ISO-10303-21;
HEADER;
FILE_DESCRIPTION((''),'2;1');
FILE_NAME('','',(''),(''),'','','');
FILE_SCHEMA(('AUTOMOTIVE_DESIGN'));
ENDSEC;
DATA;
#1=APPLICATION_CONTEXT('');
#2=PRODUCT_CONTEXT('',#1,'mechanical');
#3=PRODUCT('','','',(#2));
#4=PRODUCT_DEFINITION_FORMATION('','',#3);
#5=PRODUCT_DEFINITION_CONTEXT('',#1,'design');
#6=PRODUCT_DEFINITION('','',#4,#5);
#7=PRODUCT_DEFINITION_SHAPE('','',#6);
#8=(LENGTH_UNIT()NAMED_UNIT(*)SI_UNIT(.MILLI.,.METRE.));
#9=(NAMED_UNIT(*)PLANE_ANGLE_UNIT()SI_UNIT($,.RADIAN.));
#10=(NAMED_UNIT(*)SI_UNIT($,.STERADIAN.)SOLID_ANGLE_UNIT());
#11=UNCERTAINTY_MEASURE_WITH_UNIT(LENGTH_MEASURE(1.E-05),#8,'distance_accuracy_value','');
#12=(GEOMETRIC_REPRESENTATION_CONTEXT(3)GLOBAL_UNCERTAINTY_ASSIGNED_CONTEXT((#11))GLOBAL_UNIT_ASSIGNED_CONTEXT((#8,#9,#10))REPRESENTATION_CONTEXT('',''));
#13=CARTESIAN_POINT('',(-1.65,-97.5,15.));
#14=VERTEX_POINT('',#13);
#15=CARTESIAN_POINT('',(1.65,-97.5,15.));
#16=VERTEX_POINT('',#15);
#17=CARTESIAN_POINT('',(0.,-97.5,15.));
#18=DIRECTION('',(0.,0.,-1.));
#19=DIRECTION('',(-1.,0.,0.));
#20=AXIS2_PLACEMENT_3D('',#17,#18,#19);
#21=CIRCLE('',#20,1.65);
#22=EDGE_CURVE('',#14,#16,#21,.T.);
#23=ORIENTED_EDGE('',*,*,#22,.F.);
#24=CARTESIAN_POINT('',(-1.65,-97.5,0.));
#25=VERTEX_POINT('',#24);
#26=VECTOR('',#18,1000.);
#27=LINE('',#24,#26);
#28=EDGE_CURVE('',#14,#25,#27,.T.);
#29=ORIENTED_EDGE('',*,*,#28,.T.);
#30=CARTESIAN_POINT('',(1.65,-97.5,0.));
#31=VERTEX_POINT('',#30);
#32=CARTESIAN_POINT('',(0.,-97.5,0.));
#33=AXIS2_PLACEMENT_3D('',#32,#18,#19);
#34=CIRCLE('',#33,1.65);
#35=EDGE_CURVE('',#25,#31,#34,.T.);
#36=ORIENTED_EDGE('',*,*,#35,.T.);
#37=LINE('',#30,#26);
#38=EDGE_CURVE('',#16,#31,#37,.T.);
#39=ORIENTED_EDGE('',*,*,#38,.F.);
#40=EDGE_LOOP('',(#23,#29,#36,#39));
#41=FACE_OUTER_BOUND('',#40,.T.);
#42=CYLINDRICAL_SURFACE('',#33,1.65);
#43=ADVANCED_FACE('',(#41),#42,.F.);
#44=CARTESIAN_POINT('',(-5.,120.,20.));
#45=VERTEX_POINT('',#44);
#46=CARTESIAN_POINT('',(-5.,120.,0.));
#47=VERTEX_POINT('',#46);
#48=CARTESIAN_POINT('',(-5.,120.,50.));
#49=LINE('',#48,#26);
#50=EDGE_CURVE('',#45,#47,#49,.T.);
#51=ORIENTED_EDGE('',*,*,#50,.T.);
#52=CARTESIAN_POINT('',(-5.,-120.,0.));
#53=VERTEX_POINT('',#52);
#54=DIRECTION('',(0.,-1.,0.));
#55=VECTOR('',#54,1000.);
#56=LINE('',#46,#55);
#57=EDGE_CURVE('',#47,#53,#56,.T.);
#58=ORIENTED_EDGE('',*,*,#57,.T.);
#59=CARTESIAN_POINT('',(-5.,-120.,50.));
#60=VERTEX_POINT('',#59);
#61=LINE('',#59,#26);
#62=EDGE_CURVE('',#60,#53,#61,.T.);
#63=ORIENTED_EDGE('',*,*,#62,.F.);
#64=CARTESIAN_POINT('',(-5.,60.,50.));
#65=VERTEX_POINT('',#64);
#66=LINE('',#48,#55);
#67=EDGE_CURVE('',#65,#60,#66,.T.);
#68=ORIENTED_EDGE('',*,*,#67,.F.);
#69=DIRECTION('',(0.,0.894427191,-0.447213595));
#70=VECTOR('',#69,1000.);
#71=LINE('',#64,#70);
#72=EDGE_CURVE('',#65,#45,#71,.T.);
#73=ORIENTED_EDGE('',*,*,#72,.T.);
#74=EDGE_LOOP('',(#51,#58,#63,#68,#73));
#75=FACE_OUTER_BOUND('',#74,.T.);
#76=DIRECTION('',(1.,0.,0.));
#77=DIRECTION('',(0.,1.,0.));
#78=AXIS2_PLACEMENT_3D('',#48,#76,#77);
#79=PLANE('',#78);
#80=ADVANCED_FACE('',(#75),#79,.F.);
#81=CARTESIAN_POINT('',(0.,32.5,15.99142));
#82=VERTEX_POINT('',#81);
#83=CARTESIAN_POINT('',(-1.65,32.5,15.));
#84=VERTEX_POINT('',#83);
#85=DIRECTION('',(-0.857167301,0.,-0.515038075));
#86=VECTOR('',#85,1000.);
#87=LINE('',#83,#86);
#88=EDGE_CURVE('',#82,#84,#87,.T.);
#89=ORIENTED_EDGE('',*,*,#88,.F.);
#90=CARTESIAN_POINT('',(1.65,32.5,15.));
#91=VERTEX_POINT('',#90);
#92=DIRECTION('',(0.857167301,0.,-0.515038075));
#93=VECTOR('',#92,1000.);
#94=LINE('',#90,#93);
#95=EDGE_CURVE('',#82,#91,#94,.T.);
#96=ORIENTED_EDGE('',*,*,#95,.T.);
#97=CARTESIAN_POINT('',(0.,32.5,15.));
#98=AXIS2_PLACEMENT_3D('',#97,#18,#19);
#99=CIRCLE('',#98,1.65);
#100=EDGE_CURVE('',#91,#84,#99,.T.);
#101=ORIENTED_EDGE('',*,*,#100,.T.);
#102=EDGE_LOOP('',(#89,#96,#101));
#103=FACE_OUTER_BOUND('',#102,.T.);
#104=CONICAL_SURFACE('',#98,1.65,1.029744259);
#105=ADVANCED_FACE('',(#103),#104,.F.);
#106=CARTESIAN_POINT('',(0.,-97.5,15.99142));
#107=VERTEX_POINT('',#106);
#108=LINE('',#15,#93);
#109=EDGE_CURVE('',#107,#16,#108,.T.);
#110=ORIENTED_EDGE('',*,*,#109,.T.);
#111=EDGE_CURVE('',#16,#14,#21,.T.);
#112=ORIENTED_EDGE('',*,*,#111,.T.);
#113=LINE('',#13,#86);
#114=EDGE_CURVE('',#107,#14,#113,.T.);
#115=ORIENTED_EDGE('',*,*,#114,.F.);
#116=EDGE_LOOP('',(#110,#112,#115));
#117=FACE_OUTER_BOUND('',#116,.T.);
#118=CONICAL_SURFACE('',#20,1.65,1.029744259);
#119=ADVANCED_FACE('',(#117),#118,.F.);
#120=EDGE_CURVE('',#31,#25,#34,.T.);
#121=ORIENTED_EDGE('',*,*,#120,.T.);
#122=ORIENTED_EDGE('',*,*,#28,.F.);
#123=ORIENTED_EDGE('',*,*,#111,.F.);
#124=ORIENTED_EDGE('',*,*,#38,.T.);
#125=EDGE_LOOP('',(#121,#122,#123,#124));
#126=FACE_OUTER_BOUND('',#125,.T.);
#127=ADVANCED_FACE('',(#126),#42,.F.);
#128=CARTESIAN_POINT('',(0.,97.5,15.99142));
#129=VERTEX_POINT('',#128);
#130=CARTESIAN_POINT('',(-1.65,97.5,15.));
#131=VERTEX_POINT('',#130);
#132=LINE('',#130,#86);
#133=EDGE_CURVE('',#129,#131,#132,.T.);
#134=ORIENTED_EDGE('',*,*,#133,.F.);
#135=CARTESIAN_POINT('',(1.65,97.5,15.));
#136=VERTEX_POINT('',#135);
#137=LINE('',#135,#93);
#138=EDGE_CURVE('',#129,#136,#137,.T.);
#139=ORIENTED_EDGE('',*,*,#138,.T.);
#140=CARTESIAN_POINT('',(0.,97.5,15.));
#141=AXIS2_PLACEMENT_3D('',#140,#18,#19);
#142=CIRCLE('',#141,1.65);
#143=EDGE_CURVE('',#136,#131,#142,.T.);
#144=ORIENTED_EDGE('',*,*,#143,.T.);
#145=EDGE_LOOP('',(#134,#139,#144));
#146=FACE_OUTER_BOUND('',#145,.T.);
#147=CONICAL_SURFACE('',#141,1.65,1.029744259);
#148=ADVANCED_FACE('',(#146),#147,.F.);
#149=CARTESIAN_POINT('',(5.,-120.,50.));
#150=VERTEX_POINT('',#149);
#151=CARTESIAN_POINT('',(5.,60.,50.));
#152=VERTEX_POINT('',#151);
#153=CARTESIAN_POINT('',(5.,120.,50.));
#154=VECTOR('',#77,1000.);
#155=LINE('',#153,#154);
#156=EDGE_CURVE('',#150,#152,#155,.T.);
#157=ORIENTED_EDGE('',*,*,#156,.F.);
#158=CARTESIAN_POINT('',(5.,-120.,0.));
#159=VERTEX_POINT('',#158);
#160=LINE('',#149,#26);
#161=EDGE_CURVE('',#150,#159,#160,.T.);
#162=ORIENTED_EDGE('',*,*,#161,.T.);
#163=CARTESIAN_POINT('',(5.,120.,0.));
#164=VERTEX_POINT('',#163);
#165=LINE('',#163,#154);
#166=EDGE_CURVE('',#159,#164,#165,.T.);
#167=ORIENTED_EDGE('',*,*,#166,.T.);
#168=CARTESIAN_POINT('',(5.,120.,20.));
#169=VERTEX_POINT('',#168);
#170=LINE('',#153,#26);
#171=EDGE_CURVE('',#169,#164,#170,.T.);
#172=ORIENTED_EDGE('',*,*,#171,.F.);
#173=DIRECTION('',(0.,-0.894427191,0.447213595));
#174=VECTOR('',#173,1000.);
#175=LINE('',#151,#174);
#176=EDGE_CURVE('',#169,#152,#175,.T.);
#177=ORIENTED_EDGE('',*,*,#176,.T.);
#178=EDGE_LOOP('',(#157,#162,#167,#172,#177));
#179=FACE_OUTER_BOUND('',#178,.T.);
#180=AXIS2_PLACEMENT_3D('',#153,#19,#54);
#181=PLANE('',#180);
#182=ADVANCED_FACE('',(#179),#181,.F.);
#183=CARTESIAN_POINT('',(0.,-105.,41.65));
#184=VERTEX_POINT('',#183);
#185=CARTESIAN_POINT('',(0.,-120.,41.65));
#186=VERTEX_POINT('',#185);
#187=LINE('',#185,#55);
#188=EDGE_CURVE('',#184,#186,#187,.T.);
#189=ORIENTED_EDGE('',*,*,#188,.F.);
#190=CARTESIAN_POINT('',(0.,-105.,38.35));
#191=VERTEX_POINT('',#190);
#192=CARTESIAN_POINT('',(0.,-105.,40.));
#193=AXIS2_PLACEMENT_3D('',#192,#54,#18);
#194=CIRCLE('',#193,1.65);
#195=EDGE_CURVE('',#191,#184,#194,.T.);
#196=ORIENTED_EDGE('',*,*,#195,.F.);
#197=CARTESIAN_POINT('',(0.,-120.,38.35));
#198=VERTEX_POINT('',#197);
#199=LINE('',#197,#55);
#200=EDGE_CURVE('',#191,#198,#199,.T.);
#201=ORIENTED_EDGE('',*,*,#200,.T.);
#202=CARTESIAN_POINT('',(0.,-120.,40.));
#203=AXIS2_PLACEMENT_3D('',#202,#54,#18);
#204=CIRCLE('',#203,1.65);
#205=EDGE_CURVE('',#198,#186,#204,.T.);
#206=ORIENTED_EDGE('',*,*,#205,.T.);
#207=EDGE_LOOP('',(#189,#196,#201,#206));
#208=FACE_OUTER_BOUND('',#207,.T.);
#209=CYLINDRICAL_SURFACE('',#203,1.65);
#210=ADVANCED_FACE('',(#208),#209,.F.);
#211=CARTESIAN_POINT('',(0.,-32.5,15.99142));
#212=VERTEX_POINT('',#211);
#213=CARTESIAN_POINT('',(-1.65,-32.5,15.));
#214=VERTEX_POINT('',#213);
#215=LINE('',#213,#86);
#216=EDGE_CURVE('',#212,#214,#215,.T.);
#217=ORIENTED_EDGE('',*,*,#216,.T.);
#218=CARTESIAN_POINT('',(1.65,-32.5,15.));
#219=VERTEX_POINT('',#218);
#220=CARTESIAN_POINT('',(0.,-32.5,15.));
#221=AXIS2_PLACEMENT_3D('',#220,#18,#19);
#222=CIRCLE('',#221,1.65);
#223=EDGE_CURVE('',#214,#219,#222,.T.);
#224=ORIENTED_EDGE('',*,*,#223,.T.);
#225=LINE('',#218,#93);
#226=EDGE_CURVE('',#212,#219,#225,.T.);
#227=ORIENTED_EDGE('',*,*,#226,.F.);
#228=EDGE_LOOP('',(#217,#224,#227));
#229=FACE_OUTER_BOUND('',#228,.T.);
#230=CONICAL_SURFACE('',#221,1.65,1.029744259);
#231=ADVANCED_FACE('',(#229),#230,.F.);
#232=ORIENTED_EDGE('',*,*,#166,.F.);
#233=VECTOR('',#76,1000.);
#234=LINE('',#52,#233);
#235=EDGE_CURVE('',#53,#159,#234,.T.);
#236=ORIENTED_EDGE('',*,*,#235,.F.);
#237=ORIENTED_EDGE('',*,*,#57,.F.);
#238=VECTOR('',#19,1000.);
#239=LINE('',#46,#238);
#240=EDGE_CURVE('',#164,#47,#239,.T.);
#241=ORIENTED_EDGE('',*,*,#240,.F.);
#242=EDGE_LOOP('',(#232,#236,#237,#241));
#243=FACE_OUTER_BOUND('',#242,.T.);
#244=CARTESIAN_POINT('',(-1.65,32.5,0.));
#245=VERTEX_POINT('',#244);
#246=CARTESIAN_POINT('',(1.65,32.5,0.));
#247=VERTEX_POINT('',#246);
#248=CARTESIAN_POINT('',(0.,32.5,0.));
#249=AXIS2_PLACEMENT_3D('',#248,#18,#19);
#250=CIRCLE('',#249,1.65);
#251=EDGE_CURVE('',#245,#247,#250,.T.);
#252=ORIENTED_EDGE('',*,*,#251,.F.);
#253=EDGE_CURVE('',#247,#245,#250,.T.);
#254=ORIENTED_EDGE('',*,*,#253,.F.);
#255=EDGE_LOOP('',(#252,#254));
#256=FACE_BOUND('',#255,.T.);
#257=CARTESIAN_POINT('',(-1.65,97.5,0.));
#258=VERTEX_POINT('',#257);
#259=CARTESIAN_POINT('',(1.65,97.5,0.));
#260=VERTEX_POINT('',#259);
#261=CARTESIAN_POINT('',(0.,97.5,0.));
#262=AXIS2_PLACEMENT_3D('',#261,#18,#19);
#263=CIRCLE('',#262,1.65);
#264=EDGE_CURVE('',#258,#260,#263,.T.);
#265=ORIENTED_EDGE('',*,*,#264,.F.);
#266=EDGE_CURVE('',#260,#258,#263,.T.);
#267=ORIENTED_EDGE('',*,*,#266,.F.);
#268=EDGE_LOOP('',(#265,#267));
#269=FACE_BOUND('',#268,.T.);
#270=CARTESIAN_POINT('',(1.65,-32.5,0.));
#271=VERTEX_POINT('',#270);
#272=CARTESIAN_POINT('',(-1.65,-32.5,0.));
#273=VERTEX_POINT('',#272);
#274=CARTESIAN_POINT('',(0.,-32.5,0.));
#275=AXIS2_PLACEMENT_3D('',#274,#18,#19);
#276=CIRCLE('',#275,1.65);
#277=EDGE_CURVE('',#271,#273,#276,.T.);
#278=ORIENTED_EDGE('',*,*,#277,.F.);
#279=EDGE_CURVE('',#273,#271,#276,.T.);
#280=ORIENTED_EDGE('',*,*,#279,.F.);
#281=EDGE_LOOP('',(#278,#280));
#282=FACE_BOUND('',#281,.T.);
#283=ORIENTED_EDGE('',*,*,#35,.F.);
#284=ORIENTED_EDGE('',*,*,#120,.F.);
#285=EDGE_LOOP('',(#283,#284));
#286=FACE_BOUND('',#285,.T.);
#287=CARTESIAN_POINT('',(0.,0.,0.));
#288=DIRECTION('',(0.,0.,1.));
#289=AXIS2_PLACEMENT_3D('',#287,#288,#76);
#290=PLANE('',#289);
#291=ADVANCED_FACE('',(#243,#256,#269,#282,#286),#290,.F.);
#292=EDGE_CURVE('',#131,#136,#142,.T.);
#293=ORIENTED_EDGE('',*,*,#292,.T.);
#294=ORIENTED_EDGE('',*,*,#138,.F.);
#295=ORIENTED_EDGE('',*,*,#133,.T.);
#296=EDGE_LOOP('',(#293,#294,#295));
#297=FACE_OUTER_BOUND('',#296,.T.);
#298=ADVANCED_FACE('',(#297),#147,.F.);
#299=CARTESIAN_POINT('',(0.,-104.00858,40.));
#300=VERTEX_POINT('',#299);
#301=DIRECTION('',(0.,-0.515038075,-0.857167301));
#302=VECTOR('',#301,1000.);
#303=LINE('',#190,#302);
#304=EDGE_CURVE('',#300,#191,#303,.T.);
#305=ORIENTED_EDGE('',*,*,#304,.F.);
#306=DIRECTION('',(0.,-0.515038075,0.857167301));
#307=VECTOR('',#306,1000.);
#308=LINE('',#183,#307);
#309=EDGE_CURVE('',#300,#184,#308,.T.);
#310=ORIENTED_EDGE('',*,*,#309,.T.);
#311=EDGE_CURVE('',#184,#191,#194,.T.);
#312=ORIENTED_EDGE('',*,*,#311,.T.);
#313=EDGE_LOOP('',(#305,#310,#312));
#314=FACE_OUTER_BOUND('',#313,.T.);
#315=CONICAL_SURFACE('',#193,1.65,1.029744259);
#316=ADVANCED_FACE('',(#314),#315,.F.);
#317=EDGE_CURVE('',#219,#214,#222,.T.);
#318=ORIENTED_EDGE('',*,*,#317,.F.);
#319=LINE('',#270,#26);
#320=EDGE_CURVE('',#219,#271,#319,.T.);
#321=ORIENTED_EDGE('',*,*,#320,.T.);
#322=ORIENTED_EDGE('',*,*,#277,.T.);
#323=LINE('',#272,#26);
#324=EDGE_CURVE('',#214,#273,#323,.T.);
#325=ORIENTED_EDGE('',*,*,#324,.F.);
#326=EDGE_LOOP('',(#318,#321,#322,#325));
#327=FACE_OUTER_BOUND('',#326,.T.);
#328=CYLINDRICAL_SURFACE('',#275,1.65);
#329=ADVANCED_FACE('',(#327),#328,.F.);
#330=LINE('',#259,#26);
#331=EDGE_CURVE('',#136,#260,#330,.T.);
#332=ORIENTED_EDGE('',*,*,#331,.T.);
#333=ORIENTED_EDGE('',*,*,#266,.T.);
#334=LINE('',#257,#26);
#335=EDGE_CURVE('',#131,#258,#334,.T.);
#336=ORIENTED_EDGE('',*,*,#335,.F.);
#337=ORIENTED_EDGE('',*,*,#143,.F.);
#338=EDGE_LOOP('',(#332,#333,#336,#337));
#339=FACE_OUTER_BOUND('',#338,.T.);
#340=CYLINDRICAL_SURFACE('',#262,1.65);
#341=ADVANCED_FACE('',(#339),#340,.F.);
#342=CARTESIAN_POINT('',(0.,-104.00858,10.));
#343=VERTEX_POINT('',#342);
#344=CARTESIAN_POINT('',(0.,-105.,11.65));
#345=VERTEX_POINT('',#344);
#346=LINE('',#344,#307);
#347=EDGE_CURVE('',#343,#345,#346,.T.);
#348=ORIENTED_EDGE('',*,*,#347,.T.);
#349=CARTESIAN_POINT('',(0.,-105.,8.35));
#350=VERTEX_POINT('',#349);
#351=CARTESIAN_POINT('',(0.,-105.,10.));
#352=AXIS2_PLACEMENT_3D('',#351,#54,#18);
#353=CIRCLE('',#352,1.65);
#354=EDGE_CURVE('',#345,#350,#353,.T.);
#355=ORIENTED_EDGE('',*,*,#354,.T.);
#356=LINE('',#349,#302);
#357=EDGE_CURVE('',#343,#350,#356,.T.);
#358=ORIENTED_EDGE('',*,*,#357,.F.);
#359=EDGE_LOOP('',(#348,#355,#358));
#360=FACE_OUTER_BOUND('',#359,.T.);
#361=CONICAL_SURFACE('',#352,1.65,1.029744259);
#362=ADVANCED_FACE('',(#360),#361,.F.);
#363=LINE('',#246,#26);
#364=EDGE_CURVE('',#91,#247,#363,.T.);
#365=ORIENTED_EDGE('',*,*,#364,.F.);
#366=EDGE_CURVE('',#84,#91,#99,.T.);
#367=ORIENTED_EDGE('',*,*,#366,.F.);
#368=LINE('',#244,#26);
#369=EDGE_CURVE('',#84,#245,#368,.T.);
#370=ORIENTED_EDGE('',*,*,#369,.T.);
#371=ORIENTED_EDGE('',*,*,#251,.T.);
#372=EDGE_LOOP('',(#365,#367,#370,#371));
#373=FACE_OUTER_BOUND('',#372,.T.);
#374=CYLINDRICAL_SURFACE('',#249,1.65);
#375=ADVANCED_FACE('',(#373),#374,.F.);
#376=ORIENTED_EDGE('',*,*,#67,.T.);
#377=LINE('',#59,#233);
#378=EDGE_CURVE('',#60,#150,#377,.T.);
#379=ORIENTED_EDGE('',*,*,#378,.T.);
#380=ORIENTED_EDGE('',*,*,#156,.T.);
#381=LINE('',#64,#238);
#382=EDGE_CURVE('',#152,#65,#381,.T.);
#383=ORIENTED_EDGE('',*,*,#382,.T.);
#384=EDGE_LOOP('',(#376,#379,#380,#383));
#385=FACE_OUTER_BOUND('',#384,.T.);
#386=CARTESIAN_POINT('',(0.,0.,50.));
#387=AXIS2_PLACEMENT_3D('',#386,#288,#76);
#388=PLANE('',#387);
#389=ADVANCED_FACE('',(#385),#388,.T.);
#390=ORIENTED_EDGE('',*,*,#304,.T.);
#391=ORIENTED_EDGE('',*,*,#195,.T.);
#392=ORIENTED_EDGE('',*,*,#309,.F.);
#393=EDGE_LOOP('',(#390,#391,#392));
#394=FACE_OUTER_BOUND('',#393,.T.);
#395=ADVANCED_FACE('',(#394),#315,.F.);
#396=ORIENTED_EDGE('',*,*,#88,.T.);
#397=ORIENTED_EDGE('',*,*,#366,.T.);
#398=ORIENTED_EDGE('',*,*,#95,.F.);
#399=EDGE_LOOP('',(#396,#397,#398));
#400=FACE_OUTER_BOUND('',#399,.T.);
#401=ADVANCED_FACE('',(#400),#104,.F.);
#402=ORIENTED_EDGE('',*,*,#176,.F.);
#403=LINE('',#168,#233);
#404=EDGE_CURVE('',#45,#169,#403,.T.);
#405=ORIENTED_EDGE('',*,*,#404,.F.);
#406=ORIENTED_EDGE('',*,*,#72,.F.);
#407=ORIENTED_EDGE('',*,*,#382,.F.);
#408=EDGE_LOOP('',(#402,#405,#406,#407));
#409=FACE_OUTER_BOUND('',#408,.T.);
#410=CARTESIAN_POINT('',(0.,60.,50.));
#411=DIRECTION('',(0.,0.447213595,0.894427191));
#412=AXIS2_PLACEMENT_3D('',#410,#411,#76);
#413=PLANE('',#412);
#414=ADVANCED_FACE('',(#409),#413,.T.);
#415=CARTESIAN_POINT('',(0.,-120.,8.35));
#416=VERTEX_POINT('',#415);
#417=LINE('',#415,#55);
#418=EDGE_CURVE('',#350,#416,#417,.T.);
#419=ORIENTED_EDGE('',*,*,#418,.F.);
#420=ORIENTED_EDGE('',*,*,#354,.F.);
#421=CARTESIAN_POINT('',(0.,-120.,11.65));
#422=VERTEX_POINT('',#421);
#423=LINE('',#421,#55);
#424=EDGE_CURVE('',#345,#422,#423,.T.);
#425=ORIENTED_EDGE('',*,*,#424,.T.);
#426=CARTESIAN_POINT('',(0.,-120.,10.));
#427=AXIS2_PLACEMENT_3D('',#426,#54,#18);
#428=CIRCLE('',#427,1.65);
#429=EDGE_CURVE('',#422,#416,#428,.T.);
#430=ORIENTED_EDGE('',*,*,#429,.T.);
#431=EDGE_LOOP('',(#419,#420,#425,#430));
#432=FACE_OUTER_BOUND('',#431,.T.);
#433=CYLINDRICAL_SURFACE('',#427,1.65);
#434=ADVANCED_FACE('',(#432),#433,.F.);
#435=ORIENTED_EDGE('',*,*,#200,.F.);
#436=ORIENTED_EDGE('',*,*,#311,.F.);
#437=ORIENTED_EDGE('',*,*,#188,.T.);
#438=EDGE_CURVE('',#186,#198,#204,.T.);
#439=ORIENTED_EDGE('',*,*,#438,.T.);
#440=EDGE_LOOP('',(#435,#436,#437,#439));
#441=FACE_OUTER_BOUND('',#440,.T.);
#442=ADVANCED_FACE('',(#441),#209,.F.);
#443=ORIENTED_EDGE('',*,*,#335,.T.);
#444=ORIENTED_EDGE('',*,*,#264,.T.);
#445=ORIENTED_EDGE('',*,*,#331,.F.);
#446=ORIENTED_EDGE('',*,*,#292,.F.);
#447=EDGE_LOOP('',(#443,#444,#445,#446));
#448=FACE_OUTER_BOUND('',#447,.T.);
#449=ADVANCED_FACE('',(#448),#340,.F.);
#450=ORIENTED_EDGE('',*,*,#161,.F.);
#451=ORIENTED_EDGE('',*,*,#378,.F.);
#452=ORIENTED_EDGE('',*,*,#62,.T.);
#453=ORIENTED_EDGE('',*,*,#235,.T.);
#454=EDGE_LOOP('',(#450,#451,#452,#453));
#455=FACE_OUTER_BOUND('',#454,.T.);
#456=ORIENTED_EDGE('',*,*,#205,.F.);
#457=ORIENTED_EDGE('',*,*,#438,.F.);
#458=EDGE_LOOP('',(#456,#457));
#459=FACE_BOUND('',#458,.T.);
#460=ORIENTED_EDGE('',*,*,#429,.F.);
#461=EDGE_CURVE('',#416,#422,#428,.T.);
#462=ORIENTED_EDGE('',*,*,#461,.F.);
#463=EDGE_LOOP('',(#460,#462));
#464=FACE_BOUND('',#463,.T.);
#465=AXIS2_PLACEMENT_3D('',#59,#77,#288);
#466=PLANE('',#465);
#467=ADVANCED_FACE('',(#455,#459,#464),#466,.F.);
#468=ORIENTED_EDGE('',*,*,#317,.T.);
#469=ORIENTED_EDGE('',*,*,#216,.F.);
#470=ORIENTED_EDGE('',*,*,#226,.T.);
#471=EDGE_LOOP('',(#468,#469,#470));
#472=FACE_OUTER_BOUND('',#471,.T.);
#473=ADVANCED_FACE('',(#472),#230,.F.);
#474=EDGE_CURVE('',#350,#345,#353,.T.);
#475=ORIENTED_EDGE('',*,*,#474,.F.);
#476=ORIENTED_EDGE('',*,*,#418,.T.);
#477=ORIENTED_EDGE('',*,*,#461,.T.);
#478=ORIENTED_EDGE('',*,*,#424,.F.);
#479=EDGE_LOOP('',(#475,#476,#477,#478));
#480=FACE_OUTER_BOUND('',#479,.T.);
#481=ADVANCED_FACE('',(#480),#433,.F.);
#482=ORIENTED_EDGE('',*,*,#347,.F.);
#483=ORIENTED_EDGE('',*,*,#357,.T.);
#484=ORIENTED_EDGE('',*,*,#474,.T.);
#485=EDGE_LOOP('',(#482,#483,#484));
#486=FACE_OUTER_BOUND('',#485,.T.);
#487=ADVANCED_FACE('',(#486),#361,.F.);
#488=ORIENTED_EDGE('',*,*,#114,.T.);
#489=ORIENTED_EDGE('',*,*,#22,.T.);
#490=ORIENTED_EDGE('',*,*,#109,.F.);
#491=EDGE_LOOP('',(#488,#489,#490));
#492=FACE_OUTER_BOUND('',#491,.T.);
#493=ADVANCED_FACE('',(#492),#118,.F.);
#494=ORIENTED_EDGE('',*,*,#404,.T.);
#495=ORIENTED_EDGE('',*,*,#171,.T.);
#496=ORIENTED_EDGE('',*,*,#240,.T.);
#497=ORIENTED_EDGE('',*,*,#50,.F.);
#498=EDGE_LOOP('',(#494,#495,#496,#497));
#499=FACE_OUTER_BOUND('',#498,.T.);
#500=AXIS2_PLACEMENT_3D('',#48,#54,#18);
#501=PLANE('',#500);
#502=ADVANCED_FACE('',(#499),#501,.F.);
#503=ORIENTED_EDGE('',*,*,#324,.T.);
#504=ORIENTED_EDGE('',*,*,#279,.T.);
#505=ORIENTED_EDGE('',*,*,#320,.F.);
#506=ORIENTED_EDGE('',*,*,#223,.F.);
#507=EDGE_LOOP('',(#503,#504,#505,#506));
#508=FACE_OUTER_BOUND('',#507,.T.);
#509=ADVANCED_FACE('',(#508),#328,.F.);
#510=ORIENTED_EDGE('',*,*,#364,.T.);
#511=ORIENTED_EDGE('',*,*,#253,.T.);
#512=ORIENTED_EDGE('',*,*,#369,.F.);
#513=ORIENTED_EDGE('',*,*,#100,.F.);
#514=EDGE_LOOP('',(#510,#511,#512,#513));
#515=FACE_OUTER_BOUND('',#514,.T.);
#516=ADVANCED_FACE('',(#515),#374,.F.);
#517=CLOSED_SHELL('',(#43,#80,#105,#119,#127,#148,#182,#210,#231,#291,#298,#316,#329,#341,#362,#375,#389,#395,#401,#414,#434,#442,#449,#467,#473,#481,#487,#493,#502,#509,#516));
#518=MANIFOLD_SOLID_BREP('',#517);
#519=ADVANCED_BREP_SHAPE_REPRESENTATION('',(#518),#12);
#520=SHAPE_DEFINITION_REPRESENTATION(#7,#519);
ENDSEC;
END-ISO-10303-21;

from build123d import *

# Parameters (mm, degrees)
SKETCH_1_W             = 10
SKETCH_1_H             = 240
EXTRUDE_1_DEPTH        = 50
HOLE_WIZARD_M4_2_D     = 3.3
HOLE_WIZARD_M4_2_DEPTH = 15
HOLE_WIZARD_M4_2_TIP   = 0.991420021
HOLE_WIZARD_M4_3_D     = 3.3
HOLE_WIZARD_M4_3_DEPTH = 15
HOLE_WIZARD_M4_3_TIP   = 0.991420021
CHAMFER_1_SIZE         = 30
CHAMFER_1_SIZE2        = 60


with BuildPart() as part:
    # 草图1 → 凸台-拉伸1 (new body)
    with BuildSketch(Plane.XY):
        Rectangle(SKETCH_1_W, SKETCH_1_H)
    extrude(amount=EXTRUDE_1_DEPTH)

    # M4 螺纹孔2
    with Locations(Plane(origin=(0, 0, 0), x_dir=(-1, 0, 0), z_dir=(0, 0, -1))):
        with Locations((0, 97.5), (0, 32.5), (0, -32.5), (0, -97.5)):
            Hole(HOLE_WIZARD_M4_2_D / 2, depth=HOLE_WIZARD_M4_2_DEPTH)
            with Locations((0, 0, -(HOLE_WIZARD_M4_2_DEPTH + HOLE_WIZARD_M4_2_TIP / 2))):  # 118° drill point
                Cone(0, HOLE_WIZARD_M4_2_D / 2, HOLE_WIZARD_M4_2_TIP, mode=Mode.SUBTRACT)

    # M4 螺纹孔3
    with Locations(Plane(origin=(0, -120, 0), x_dir=(-1, 0, 0), z_dir=(0, -1, 0))):
        with Locations((0, -10), (0, -40)):
            Hole(HOLE_WIZARD_M4_3_D / 2, depth=HOLE_WIZARD_M4_3_DEPTH)
            with Locations((0, 0, -(HOLE_WIZARD_M4_3_DEPTH + HOLE_WIZARD_M4_3_TIP / 2))):  # 118° drill point
                Cone(0, HOLE_WIZARD_M4_3_D / 2, HOLE_WIZARD_M4_3_TIP, mode=Mode.SUBTRACT)

    # 倒角1
    chamfer_1_edges = [part.edges().sort_by_distance(p)[0] for p in [
        (0, 120, 50),
    ]]
    chamfer_1_side = [part.faces().sort_by_distance(p)[0] for p in [
        (0, 120, 25),
    ]]
    chamfer(chamfer_1_edges, length=CHAMFER_1_SIZE, length2=CHAMFER_1_SIZE2, reference=chamfer_1_side[0])


solid = part.part
